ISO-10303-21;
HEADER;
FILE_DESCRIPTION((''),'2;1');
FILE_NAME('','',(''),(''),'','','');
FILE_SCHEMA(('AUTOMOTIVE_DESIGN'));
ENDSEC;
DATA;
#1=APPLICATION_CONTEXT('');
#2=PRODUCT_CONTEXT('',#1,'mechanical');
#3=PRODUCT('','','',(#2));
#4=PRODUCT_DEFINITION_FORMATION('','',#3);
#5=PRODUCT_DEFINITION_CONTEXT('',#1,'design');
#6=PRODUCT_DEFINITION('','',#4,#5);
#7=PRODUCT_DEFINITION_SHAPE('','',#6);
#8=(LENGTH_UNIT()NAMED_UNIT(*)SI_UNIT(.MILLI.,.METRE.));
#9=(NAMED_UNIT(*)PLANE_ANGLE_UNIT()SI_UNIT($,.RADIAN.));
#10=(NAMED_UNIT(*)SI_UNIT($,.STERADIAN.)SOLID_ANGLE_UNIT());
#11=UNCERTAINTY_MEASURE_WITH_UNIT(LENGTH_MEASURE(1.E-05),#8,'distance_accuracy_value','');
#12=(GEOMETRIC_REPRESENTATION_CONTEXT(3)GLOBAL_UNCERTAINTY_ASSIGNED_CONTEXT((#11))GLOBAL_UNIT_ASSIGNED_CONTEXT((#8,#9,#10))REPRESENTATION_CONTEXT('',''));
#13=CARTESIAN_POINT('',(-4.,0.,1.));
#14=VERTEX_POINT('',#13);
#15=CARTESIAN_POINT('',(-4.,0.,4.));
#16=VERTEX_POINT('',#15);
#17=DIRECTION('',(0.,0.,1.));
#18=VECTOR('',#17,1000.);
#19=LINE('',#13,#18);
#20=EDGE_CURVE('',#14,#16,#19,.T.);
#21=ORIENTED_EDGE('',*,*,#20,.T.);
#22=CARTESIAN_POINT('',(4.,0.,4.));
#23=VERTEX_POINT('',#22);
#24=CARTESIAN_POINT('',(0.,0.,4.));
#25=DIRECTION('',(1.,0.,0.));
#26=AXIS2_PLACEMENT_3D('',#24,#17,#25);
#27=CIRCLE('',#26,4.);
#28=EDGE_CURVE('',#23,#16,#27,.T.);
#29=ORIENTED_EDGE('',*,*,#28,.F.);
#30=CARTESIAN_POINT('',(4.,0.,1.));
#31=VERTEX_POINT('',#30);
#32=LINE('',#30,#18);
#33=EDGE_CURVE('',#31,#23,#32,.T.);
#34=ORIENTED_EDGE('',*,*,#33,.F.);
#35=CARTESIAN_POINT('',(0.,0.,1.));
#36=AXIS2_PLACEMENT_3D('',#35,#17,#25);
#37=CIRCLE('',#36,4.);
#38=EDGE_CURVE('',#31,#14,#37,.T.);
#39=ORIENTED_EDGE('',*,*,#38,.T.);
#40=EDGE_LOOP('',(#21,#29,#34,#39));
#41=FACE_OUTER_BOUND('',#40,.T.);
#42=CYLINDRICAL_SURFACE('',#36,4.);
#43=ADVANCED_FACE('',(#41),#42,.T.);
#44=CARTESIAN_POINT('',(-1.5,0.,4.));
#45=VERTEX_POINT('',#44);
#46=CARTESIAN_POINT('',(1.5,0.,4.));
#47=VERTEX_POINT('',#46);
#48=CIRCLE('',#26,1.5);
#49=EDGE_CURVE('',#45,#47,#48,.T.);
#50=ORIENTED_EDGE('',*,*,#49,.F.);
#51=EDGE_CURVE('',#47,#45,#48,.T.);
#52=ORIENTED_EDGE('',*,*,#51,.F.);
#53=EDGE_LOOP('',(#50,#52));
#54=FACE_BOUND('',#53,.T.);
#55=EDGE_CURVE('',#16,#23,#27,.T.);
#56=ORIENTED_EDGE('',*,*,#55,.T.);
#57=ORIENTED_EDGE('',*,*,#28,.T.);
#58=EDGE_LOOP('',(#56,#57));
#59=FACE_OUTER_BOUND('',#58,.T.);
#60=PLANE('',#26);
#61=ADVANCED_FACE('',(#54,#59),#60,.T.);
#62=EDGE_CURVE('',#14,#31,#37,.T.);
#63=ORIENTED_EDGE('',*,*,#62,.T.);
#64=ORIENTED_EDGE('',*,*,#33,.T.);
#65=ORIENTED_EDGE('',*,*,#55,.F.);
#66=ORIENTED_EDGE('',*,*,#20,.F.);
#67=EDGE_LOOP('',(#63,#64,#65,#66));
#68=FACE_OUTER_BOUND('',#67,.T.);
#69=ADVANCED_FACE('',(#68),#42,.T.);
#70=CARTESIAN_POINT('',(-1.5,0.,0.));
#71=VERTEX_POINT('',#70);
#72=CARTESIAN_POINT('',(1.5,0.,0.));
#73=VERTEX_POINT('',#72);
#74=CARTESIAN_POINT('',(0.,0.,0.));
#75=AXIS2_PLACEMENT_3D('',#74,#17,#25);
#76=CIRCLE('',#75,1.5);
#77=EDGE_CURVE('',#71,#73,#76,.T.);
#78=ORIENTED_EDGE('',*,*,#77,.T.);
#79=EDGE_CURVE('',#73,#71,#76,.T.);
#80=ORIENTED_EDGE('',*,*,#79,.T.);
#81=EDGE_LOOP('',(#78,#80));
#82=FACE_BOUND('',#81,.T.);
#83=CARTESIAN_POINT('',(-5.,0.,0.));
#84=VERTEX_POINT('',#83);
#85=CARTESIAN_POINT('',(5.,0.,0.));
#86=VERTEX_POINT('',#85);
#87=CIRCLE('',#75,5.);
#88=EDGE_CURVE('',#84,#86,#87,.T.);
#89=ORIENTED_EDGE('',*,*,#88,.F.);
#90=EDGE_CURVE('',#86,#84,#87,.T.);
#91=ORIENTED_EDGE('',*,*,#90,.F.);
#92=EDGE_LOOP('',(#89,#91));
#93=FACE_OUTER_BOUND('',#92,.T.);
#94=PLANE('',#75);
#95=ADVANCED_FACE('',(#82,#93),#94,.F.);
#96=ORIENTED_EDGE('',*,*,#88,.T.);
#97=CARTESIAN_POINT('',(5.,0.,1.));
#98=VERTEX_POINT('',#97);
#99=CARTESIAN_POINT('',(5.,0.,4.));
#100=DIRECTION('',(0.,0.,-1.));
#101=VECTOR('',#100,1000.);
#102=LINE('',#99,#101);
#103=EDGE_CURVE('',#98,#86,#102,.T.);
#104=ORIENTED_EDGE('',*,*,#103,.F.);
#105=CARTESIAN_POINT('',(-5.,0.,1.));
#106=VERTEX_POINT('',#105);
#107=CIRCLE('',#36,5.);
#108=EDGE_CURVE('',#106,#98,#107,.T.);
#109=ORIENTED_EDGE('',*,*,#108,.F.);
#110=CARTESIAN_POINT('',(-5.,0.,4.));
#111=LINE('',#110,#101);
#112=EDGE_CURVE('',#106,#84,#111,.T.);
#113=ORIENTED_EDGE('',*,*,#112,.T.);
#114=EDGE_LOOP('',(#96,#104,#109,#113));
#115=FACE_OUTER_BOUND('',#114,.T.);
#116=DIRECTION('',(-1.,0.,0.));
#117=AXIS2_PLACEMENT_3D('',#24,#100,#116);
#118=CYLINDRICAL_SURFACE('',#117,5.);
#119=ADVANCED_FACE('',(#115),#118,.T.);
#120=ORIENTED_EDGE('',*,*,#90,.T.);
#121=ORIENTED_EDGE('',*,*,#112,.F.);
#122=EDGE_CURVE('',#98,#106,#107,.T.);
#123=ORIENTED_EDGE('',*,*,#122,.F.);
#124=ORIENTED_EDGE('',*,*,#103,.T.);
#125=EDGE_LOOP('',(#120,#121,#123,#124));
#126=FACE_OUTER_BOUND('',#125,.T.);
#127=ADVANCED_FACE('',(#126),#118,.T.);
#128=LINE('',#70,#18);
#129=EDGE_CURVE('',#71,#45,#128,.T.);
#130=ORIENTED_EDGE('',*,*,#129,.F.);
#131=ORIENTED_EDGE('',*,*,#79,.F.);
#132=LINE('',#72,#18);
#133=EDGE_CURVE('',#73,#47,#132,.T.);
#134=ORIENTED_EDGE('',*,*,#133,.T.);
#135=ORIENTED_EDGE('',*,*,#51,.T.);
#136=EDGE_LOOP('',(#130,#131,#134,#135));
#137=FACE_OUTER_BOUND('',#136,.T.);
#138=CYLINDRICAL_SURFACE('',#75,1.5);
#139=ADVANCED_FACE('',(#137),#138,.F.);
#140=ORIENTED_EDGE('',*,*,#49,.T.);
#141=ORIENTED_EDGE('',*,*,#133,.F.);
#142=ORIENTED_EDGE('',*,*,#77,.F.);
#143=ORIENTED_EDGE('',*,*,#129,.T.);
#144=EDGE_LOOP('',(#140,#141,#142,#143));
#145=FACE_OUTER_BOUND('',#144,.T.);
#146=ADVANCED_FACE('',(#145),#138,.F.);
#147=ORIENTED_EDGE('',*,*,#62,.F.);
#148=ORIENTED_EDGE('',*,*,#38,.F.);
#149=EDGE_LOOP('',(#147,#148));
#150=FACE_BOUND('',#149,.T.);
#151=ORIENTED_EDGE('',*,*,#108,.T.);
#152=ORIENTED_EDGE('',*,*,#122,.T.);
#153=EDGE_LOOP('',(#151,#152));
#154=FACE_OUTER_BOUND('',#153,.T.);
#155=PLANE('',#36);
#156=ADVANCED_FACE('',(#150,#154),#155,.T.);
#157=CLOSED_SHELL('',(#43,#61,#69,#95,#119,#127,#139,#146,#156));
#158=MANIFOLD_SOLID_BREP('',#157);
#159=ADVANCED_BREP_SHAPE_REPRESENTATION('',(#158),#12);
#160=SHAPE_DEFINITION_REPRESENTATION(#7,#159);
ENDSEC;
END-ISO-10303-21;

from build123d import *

# Parameters (mm, degrees)
SKETCH1_R               = 5
BOSS_EXTRUDE1_DEPTH     = 4
CUT_EXTRUDE1_START      = -3
SKETCH2_R               = 5
SKETCH2_R_2             = 4
CUT_EXTRUDE1_DEPTH      = 3
CUT_EXTRUDE2_DEPTH      = 9.124038405
CUT_EXTRUDE2_DEPTH_BACK = 9.124038405
SKETCH3_R               = 1.5


with BuildPart() as part:
    # Sketch1 → Boss-Extrude1 (new body)
    with BuildSketch(Plane.XY):
        Circle(SKETCH1_R)
    extrude(amount=BOSS_EXTRUDE1_DEPTH)

    # Sketch2 → Cut-Extrude1 (cut)
    with BuildSketch(Plane.XY.offset(4).offset(CUT_EXTRUDE1_START)):
        Circle(SKETCH2_R)
        Circle(SKETCH2_R_2, mode=Mode.SUBTRACT)
    extrude(amount=CUT_EXTRUDE1_DEPTH, mode=Mode.SUBTRACT)

    # Sketch3 → Cut-Extrude2 (cut, two sides: drawn at the far end of the back side and taken through both)
    with BuildSketch(Plane.XY.offset(4).offset(-CUT_EXTRUDE2_DEPTH_BACK)):
        Circle(SKETCH3_R)
    extrude(amount=CUT_EXTRUDE2_DEPTH + CUT_EXTRUDE2_DEPTH_BACK, mode=Mode.SUBTRACT)


solid = part.part
